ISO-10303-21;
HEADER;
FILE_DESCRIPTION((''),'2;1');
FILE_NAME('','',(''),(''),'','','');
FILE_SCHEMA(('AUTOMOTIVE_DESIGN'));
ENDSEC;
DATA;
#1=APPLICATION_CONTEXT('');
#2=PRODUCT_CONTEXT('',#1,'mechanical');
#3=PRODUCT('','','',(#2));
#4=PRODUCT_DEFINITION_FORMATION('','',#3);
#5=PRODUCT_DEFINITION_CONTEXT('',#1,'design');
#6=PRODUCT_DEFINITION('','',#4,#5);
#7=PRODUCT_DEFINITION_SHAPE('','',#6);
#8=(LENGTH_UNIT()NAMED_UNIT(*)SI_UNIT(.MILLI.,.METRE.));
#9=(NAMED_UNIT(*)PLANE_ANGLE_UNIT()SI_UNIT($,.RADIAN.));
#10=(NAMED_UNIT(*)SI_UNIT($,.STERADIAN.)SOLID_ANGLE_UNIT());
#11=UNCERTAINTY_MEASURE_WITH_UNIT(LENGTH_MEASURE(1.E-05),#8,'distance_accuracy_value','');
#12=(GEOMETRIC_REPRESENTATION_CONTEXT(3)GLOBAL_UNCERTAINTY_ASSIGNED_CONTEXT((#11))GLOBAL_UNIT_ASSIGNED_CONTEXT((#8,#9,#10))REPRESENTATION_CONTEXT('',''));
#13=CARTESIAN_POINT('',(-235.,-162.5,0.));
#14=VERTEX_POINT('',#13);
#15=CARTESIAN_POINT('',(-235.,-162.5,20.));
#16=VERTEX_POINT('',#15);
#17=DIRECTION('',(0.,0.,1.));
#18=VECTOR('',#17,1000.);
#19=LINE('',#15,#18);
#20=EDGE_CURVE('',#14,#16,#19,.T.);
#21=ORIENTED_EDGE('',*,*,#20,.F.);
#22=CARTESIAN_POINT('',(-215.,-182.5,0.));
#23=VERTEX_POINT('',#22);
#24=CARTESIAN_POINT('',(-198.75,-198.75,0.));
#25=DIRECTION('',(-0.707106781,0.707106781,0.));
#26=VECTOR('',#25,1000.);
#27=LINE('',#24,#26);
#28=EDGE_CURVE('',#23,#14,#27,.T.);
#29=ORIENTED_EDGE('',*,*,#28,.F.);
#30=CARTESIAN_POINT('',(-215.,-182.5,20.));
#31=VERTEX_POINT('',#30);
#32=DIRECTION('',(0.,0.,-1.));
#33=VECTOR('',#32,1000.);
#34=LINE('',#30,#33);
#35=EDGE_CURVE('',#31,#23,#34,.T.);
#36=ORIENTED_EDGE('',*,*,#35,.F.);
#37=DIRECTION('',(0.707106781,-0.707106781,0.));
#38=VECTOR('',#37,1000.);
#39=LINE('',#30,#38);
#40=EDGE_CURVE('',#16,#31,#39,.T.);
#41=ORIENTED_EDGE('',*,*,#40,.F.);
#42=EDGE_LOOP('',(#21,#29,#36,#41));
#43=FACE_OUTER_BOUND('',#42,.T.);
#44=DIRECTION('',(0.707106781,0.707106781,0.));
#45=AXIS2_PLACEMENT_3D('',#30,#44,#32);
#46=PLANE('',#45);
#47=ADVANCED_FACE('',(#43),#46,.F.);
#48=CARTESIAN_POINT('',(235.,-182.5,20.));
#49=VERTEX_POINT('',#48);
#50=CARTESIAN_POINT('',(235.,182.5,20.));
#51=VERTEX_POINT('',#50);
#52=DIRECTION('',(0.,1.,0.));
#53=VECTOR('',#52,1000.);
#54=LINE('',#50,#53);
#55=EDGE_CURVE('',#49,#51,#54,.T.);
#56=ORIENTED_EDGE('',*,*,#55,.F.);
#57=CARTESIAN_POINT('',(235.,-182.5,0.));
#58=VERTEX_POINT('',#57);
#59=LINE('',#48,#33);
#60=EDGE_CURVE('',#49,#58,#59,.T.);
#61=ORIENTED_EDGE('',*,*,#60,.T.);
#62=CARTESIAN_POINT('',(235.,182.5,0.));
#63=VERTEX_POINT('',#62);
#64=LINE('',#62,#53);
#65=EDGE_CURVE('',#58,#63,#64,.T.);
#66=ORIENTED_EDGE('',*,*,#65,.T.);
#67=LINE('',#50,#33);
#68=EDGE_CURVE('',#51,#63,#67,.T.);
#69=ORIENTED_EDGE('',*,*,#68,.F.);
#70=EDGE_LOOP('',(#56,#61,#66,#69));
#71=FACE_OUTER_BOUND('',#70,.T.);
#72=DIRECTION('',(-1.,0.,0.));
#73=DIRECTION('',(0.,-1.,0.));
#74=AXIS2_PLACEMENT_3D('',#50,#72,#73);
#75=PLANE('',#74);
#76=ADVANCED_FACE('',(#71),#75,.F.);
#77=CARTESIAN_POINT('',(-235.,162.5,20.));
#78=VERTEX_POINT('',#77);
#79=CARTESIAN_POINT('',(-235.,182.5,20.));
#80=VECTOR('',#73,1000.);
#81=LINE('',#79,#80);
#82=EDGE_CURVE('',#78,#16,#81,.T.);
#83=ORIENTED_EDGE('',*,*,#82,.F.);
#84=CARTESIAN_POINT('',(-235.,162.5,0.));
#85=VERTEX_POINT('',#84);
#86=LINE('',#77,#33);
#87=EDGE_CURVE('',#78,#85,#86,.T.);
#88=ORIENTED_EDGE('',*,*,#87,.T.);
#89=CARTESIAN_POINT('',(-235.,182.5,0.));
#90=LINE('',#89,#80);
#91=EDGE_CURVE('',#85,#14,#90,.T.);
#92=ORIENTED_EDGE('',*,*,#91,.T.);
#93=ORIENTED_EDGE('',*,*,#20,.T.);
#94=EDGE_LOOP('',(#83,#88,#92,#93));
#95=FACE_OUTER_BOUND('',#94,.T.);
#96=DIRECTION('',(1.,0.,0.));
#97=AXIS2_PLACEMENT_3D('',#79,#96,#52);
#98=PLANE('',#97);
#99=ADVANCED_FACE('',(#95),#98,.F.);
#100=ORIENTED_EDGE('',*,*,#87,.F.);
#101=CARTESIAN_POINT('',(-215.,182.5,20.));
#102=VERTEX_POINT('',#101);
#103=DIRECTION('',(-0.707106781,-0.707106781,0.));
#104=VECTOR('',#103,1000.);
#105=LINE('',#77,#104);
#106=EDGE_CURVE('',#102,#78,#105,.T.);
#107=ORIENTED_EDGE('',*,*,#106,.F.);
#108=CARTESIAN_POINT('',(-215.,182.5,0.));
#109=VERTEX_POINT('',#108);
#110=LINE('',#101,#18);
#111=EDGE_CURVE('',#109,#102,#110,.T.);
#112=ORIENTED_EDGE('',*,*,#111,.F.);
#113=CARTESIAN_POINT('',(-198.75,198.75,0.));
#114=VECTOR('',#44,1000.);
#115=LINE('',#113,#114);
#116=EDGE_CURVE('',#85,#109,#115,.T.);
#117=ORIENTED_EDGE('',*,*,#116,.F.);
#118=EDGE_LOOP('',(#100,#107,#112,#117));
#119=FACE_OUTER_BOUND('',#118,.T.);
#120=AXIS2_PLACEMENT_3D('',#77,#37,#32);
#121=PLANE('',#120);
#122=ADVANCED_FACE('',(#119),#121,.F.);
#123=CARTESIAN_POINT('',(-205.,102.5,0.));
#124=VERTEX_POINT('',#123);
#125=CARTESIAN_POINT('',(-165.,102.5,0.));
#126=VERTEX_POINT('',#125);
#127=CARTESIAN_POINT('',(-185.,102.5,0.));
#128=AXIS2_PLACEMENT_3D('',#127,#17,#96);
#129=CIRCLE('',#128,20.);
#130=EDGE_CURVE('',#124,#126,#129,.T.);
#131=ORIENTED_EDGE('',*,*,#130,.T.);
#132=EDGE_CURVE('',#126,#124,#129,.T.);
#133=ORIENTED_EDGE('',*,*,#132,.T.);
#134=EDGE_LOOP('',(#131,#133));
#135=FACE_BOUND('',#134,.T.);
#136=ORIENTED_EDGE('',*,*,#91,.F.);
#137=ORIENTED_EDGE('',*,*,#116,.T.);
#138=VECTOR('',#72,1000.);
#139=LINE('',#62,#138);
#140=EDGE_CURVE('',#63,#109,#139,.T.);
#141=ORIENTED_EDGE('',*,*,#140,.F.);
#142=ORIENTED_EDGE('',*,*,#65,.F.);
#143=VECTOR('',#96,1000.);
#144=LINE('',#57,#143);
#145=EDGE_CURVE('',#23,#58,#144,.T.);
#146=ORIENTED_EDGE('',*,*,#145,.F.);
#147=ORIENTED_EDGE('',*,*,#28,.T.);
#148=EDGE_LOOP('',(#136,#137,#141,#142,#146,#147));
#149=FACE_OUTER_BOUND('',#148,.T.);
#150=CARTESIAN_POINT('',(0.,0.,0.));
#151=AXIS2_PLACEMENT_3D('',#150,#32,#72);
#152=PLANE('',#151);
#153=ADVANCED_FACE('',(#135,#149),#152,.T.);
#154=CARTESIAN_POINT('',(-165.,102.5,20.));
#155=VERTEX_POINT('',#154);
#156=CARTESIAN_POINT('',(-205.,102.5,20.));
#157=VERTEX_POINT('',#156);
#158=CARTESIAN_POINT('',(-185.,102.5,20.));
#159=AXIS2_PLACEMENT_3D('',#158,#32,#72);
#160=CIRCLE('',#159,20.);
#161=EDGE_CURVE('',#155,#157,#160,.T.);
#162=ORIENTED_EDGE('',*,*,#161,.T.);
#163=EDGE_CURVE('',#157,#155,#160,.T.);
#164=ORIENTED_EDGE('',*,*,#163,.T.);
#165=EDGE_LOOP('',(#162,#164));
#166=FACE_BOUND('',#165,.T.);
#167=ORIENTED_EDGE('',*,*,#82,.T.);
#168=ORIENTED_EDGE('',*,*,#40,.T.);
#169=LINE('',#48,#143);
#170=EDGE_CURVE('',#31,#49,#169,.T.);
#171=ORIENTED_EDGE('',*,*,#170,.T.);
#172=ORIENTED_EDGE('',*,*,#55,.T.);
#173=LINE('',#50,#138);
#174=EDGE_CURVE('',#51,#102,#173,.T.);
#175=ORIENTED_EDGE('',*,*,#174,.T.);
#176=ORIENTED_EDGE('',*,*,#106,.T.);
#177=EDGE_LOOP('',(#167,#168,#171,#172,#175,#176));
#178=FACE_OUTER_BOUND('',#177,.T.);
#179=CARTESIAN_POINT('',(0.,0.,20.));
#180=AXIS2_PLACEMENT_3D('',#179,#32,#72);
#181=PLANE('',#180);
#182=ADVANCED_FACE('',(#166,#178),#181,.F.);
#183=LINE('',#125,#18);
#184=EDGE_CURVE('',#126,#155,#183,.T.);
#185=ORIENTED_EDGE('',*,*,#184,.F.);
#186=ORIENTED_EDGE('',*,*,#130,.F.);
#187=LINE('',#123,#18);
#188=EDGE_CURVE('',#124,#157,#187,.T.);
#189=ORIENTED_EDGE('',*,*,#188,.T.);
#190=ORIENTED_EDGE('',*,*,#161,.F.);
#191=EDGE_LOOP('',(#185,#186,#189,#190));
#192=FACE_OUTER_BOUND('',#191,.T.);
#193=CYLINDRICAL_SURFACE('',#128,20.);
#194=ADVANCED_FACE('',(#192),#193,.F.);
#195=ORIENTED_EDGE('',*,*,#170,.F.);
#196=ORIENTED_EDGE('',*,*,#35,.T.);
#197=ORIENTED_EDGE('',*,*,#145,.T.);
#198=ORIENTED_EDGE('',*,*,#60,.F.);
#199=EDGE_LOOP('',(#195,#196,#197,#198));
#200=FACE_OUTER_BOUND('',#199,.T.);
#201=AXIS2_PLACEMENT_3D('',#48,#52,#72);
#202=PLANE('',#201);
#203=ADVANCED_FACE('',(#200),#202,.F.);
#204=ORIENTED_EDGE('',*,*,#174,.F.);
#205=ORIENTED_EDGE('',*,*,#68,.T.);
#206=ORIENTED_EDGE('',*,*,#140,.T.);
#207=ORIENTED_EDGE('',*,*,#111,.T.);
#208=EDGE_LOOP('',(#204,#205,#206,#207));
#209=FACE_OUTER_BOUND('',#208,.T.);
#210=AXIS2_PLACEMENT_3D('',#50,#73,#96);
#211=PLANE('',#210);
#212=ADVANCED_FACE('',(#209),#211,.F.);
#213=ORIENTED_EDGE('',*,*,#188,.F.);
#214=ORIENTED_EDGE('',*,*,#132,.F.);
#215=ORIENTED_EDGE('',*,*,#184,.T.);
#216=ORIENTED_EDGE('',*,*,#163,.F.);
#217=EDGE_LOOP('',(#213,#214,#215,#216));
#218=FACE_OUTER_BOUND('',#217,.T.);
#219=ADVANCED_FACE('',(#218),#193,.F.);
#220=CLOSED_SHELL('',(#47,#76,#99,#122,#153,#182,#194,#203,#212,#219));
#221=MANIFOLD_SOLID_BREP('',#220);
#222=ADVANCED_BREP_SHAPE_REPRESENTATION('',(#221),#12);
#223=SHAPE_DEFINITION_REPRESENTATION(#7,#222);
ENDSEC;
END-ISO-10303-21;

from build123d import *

# Parameters (mm, degrees)
SKETCH1_W               = 470
SKETCH1_H               = 365
BOSS_EXTRUDE1_DEPTH     = 20
CHAMFER1_SIZE           = 20
CUT_EXTRUDE1_DEPTH      = 299.213430281
CUT_EXTRUDE1_DEPTH_BACK = 299.213430281
SKETCH2_R               = 20
CHAMFER2_SIZE           = 20


with BuildPart() as part:
    # Sketch1 → Boss-Extrude1 (new body)
    with BuildSketch(Plane.XY):
        Rectangle(SKETCH1_W, SKETCH1_H)
    extrude(amount=BOSS_EXTRUDE1_DEPTH)

    # Chamfer1
    chamfer1_edges = [part.edges().sort_by_distance(p)[0] for p in [
        (-235, 182.5, 10),
    ]]
    chamfer(chamfer1_edges, length=CHAMFER1_SIZE)

    # Sketch2 → Cut-Extrude1 (cut, two sides: drawn at the far end of the back side and taken through both)
    with BuildSketch(Plane.XY.offset(20).offset(-CUT_EXTRUDE1_DEPTH_BACK)):
        with Locations((-185, 102.5)):
            Circle(SKETCH2_R)
    extrude(amount=CUT_EXTRUDE1_DEPTH + CUT_EXTRUDE1_DEPTH_BACK, mode=Mode.SUBTRACT)

    # Chamfer2
    chamfer2_edges = [part.edges().sort_by_distance(p)[0] for p in [
        (-235, -182.5, 10),
    ]]
    chamfer(chamfer2_edges, length=CHAMFER2_SIZE)


solid = part.part
